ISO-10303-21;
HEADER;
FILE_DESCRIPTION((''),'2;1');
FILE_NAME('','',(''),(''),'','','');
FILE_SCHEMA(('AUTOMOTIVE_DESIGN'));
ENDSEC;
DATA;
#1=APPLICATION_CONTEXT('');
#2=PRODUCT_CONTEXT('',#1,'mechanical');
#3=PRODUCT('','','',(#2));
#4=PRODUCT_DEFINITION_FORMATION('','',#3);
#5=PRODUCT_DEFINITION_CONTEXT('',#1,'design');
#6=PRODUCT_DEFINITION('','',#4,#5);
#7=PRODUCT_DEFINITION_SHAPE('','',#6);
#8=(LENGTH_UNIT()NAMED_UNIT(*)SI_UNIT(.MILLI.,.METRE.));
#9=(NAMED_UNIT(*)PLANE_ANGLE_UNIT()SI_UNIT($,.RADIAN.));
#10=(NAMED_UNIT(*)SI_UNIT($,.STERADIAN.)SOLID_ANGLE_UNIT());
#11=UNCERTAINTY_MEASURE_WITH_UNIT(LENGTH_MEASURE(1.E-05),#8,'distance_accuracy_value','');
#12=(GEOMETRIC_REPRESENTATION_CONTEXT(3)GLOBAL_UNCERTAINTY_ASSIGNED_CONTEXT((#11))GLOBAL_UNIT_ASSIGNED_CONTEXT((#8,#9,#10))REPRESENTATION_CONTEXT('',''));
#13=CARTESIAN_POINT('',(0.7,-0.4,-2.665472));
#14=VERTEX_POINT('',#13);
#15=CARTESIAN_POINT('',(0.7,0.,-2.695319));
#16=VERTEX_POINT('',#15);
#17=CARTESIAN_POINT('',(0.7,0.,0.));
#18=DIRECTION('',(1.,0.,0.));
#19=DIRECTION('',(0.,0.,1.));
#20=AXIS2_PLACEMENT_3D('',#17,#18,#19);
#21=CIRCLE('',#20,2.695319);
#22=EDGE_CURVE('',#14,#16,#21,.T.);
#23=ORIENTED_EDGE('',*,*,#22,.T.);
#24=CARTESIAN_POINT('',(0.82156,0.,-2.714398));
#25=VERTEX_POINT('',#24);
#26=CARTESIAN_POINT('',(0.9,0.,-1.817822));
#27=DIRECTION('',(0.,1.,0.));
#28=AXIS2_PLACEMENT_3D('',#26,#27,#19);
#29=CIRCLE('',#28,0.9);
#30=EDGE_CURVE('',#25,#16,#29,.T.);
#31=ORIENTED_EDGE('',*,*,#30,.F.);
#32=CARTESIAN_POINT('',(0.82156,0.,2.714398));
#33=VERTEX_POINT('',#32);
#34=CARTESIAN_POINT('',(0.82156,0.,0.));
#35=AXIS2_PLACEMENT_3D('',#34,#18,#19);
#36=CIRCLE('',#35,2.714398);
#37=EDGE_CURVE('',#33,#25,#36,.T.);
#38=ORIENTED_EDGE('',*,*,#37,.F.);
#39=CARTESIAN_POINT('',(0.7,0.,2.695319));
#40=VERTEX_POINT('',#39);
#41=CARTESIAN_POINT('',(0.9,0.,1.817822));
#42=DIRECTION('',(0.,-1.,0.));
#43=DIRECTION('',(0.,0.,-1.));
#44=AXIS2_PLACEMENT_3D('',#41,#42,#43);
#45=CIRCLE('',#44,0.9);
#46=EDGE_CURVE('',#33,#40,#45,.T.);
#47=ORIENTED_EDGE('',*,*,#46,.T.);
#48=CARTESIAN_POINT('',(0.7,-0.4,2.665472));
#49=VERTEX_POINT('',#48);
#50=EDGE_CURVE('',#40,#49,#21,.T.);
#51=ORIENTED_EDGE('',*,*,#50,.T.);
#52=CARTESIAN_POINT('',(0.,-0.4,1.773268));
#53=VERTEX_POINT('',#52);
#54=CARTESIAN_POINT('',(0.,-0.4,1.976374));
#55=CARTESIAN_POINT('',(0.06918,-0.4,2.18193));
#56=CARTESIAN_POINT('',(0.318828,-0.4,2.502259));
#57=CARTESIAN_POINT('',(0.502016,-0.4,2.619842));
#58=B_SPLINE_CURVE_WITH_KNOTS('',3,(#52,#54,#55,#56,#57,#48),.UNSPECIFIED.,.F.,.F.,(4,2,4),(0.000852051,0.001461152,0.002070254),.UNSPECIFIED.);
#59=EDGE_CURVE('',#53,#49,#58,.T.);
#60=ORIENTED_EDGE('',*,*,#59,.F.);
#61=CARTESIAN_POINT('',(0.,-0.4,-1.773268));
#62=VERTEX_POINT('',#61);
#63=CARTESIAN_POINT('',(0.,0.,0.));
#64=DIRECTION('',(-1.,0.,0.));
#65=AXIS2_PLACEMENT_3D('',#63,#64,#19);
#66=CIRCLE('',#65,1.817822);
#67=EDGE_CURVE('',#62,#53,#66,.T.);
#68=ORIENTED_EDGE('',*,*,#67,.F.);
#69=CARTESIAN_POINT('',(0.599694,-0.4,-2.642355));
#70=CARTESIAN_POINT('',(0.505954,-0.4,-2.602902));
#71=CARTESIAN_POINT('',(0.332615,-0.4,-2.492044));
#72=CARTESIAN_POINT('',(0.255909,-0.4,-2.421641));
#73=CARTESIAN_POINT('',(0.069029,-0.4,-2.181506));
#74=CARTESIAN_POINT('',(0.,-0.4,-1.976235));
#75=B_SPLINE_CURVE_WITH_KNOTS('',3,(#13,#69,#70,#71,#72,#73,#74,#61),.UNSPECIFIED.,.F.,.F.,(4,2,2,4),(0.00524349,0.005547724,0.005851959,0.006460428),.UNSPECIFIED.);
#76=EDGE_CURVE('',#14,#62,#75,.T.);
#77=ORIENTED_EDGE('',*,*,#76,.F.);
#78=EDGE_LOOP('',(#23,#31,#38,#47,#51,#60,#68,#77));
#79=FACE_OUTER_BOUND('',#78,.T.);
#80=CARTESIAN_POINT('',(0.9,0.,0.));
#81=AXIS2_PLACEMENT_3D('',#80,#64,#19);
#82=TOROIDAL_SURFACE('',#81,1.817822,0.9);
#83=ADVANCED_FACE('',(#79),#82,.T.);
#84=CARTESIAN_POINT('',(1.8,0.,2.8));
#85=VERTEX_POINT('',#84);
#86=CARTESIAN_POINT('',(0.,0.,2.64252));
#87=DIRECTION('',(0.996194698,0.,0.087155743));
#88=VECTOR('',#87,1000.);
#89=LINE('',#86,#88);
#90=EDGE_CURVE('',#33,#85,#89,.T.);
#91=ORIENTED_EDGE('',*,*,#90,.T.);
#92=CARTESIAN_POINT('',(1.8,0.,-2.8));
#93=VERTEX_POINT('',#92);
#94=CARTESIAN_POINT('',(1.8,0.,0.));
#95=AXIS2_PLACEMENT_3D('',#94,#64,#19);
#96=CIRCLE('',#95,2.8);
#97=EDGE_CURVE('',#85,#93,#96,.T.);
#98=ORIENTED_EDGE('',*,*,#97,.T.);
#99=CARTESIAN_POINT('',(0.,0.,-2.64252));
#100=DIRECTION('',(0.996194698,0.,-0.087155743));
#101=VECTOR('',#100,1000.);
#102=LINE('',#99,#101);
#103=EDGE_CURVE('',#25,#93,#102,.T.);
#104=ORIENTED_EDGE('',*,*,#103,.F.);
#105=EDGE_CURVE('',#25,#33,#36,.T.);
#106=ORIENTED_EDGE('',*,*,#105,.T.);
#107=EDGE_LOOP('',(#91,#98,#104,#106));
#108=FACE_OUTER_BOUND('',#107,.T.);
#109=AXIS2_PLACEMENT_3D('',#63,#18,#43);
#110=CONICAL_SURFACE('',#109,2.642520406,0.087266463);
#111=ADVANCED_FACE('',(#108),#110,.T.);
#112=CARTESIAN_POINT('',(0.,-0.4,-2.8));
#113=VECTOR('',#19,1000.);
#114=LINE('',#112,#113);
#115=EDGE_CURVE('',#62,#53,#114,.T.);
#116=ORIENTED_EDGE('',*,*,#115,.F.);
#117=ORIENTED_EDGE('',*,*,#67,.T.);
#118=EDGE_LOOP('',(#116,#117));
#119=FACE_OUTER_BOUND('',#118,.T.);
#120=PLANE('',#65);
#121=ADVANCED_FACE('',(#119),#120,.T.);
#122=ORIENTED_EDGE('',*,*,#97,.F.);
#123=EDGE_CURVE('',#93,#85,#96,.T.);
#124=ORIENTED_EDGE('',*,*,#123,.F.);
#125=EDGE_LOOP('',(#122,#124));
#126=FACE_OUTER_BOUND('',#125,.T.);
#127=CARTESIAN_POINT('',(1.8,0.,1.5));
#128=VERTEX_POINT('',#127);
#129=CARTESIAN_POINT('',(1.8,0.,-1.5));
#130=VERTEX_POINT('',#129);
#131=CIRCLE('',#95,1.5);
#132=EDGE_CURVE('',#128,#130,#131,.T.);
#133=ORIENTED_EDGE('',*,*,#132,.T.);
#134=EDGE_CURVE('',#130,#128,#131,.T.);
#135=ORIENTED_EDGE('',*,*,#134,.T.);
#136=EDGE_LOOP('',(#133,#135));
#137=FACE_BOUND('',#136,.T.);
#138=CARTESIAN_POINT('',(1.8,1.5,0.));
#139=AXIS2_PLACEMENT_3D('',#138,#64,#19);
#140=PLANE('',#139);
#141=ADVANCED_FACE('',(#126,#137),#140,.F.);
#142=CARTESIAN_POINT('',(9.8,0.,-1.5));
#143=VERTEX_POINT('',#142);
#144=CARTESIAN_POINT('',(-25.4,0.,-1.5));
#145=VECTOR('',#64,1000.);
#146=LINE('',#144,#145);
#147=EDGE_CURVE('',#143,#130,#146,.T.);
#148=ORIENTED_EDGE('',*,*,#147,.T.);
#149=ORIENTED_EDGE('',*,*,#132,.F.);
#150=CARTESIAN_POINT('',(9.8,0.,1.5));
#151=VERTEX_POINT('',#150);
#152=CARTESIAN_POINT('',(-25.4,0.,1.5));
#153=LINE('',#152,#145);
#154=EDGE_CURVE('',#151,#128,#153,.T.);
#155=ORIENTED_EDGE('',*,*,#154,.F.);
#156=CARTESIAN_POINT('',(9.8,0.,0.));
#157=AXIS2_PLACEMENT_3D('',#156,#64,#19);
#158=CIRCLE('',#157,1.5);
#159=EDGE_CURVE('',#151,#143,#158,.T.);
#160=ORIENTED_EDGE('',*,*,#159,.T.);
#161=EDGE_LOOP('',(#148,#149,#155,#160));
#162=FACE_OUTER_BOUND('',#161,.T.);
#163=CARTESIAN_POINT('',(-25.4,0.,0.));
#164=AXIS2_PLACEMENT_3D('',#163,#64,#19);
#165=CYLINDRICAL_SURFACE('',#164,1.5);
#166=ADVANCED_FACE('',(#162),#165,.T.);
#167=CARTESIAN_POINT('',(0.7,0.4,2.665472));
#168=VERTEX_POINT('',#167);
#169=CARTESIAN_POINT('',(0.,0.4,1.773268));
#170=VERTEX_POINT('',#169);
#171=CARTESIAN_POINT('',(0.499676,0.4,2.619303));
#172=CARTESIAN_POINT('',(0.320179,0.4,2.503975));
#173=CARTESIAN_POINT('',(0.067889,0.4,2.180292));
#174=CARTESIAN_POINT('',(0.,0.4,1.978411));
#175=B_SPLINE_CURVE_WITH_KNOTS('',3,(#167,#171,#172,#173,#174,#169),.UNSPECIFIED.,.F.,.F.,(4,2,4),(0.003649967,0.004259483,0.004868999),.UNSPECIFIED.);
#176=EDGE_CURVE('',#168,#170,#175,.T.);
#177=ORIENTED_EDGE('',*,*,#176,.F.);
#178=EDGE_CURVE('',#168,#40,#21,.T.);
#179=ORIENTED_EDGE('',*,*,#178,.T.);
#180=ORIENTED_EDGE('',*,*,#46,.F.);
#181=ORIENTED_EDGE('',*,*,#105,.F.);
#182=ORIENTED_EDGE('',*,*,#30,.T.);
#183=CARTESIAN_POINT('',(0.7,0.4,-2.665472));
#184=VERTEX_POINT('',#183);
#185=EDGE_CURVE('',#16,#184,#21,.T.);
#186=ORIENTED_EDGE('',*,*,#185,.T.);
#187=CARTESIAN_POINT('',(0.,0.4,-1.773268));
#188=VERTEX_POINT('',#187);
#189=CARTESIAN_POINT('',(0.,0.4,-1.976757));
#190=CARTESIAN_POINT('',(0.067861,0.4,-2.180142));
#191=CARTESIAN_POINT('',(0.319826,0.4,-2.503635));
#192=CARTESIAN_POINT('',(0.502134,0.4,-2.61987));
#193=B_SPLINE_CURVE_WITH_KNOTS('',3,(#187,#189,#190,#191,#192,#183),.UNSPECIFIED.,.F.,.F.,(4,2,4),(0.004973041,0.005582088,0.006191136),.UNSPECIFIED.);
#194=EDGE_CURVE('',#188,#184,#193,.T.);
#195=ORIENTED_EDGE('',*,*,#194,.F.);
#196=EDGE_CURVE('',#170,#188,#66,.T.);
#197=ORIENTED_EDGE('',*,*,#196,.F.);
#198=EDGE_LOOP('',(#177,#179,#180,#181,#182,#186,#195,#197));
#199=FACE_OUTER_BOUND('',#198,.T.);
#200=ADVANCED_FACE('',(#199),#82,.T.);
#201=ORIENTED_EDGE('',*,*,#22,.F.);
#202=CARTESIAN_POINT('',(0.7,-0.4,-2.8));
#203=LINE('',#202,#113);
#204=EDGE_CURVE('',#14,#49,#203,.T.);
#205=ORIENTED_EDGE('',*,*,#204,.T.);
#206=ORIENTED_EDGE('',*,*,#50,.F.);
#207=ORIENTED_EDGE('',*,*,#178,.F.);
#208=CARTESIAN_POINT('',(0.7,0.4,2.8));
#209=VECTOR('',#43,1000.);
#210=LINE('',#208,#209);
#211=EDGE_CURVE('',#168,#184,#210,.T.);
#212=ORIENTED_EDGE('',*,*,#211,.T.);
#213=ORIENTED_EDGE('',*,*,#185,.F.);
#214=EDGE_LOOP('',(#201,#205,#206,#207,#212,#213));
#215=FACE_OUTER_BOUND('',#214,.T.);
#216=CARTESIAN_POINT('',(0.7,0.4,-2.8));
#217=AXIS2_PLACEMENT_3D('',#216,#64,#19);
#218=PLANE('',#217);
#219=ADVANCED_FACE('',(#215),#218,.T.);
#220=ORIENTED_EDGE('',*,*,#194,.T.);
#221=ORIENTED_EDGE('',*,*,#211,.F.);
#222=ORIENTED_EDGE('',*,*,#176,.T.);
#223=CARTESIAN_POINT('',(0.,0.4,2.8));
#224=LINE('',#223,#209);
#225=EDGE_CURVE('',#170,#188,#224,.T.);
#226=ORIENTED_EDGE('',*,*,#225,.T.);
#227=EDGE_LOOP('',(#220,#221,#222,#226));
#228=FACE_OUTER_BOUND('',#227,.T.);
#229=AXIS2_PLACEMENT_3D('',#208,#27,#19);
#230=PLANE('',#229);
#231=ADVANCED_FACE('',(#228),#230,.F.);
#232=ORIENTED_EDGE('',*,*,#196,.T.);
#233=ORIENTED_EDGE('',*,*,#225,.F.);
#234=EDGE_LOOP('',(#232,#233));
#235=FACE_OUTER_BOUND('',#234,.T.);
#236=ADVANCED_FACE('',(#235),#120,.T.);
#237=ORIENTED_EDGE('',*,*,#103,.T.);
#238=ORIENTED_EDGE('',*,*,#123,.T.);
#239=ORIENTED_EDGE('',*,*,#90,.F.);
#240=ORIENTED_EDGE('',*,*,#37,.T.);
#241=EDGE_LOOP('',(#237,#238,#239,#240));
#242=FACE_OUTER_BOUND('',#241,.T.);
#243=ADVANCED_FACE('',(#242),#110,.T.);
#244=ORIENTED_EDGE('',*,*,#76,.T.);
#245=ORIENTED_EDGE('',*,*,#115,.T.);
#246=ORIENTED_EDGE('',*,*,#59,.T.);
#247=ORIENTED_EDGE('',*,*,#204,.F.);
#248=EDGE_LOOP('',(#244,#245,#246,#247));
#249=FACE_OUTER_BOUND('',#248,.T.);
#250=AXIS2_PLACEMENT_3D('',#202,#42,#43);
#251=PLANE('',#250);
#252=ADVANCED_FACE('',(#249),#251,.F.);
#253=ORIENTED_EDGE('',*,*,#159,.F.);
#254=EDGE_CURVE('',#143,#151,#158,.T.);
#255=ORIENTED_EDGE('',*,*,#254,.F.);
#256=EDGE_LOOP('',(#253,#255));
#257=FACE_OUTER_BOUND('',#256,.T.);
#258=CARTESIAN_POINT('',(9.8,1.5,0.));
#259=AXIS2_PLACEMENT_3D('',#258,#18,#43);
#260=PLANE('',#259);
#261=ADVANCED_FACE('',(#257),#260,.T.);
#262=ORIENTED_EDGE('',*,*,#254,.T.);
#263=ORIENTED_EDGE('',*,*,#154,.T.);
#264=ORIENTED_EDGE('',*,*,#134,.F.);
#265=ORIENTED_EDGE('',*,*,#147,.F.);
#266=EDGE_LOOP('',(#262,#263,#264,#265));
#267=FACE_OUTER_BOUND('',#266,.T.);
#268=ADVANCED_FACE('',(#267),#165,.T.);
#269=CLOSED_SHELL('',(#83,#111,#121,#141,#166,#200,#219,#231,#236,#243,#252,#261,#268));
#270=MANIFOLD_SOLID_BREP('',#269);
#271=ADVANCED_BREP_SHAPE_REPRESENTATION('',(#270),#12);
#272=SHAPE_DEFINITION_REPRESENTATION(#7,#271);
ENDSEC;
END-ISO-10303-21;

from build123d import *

# Parameters (mm, degrees)
FILLET2_R  = 0.9
SKETCH2_W  = 5.6
SKETCH2_H  = 0.8
SLOT_DEPTH = 0.7


with BuildPart() as part:
    # BodySke → Base-Revolve (revolve)
    with BuildSketch(Plane.XY, mode=Mode.PRIVATE) as base_revolve_sk:
        Polygon((1.8, 1.5), (1.8, 2.8), (0, 2.642520406), (0, 0), (9.8, 0), (9.8, 1.5), align=None)
    revolve(base_revolve_sk.sketch.rotate(Axis((-25.4, 0, 0), (1, 0, 0)), 90), axis=Axis((-25.4, 0, 0), (1, 0, 0)))

    # Fillet2
    fillet2_edges = [part.edges().sort_by_distance(p)[0] for p in [
        (0, 0, -2.642520406),
    ]]
    fillet(fillet2_edges, radius=FILLET2_R)

    # Sketch2 → Slot (cut)
    with BuildSketch(Plane(origin=(0, 0, 0), x_dir=(0, 0, -1), z_dir=(1, 0, 0))):
        Rectangle(SKETCH2_W, SKETCH2_H)
    extrude(amount=SLOT_DEPTH, mode=Mode.SUBTRACT)


solid = part.part
